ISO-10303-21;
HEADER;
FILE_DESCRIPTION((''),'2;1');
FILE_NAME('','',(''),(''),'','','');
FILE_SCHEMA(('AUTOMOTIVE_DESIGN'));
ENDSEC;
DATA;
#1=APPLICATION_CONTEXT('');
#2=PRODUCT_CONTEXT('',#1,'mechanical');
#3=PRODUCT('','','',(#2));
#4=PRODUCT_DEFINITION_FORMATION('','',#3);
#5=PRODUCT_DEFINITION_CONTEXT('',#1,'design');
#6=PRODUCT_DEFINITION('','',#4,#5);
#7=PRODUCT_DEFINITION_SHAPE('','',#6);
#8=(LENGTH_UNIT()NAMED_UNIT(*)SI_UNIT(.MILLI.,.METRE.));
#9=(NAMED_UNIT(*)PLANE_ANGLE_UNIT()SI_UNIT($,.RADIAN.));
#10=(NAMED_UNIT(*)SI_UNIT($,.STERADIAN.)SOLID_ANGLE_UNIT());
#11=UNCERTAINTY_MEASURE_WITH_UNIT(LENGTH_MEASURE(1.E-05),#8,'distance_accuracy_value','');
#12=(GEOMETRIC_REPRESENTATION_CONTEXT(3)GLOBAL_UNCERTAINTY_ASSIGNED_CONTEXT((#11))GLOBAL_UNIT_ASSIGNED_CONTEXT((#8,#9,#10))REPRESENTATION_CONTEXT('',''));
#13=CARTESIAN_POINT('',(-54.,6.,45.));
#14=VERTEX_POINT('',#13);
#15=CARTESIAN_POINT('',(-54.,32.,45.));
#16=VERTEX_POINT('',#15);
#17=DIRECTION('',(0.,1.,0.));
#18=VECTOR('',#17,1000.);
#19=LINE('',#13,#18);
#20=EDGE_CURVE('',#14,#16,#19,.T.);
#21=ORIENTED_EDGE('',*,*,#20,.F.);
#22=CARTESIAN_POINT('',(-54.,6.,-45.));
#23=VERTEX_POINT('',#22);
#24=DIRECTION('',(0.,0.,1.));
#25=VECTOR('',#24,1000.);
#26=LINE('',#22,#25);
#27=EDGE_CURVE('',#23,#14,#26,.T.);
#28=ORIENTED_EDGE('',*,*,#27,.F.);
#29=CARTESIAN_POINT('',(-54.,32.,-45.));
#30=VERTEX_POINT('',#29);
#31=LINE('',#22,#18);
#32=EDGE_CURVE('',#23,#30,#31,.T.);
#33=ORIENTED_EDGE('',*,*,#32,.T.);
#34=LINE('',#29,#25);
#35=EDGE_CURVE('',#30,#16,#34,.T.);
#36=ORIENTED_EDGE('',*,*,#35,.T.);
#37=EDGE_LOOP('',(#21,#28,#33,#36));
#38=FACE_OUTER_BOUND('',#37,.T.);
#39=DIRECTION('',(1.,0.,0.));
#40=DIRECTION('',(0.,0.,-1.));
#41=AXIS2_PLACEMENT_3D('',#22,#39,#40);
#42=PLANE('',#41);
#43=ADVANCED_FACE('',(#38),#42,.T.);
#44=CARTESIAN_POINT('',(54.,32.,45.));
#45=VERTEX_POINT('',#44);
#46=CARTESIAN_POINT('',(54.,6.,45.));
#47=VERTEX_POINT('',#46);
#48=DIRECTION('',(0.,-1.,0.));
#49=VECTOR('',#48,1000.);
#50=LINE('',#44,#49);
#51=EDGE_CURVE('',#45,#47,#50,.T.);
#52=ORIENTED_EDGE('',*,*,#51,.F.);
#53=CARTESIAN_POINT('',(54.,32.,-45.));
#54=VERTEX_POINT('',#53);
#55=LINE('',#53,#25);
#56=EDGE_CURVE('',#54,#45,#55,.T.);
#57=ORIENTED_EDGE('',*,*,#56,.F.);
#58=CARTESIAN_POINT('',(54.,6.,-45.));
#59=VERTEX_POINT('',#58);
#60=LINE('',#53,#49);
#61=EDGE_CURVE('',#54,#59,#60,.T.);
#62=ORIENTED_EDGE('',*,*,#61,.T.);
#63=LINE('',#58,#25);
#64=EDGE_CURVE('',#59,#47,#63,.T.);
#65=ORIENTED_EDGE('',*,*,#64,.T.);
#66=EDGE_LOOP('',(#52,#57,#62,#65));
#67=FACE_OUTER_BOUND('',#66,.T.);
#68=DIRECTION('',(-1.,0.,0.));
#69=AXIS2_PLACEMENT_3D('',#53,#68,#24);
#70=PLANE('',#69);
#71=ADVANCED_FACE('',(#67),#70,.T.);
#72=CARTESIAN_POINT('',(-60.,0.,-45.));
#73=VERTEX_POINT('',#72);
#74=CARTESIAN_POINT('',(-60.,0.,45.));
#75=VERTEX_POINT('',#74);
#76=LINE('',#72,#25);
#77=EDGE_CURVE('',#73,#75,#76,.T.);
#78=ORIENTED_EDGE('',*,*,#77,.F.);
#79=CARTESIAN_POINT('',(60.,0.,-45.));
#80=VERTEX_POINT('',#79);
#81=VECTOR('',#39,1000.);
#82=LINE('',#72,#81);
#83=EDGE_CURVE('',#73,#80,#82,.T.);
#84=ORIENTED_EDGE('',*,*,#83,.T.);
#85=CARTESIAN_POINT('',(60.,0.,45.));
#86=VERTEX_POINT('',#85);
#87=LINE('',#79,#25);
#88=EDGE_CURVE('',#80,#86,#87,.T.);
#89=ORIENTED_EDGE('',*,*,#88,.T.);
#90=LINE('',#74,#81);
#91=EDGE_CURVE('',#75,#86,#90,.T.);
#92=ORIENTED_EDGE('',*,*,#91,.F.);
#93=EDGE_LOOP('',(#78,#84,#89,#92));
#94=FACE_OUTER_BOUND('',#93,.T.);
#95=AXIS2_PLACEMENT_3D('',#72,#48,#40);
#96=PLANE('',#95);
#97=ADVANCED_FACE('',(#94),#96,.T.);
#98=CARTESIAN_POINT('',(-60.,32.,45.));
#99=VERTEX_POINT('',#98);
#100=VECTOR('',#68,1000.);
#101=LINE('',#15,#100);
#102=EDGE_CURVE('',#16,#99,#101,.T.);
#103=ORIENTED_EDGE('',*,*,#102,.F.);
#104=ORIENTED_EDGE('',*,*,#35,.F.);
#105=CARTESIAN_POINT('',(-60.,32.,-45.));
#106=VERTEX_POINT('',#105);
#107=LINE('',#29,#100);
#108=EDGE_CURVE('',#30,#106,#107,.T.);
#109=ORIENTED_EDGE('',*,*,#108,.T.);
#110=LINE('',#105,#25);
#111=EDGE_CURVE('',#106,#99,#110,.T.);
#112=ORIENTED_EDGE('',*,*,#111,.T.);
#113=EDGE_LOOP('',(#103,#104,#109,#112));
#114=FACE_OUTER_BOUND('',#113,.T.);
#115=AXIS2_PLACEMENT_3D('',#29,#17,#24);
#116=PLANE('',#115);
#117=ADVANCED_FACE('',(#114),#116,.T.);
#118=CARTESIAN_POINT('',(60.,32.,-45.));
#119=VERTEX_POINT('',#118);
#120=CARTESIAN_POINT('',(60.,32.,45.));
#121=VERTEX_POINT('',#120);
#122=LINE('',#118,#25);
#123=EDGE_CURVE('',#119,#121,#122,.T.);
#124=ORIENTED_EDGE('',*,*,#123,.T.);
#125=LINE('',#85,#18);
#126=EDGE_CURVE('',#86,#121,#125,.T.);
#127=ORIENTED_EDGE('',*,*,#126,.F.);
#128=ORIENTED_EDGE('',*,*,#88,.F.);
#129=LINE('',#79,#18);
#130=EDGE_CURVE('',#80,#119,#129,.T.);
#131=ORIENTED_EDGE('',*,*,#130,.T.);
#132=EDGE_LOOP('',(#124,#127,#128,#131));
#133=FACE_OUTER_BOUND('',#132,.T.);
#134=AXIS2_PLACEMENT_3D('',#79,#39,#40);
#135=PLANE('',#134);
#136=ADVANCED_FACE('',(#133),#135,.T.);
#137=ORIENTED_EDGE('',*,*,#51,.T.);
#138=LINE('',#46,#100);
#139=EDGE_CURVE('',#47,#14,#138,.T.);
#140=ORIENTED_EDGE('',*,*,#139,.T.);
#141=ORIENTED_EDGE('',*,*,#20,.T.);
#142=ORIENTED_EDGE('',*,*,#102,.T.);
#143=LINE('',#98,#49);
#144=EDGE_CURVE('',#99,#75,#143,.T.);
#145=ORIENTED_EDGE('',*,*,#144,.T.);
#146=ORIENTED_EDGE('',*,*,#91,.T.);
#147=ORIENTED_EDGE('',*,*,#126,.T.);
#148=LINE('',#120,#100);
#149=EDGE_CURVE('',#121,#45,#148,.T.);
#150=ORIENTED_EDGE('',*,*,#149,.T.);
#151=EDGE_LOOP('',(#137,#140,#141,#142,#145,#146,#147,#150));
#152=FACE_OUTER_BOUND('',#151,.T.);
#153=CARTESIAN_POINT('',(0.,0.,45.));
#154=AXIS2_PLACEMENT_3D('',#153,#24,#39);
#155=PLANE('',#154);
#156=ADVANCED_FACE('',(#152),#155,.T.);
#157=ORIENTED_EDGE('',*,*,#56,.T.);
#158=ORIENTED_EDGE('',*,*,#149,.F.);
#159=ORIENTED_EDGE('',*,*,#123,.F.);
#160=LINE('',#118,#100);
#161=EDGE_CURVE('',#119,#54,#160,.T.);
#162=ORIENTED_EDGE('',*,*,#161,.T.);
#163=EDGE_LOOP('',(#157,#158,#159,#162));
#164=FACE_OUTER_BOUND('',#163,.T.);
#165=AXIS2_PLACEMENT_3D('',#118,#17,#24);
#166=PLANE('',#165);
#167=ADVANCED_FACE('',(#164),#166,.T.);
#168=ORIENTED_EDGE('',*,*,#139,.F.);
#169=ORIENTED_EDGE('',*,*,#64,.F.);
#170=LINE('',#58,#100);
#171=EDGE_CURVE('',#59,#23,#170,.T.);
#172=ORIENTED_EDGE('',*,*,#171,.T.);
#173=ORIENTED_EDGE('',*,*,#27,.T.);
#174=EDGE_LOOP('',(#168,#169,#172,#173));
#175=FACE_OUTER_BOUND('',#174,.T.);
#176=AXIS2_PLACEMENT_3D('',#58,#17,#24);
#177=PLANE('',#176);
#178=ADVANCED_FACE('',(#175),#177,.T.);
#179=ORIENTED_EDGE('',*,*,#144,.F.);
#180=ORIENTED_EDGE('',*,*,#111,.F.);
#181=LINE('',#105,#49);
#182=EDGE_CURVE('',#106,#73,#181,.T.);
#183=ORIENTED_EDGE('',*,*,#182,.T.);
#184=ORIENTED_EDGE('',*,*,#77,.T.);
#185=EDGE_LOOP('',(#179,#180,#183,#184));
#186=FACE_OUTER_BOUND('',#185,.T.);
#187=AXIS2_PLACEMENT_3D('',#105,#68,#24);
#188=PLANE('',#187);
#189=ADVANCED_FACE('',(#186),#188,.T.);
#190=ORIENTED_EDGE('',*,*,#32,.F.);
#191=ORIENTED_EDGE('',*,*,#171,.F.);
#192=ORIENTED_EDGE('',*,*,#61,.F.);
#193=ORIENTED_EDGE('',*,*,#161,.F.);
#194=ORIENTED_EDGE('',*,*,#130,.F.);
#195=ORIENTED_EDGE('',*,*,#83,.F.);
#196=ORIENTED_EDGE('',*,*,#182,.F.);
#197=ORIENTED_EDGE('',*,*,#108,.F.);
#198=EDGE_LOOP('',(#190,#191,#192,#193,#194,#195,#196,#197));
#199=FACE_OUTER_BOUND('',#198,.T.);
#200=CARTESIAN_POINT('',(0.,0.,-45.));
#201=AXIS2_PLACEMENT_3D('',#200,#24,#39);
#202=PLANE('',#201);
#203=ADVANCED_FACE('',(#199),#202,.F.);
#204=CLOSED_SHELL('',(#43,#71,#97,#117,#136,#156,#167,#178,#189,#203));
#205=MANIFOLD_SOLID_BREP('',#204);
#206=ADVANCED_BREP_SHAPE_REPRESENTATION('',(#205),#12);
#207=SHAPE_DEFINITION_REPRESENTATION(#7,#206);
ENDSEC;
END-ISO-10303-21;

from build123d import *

# Parameters (mm, degrees)
EXTRUDE_1_DEPTH = 45


with BuildPart() as part:
    # 草图1 → 凸台-拉伸1 (new, symmetric)
    with BuildSketch(Plane.XY):
        Polygon((-60, 0), (60, 0), (60, 32), (54, 32), (54, 6), (-54, 6), (-54, 32), (-60, 32), align=None)
    extrude(amount=EXTRUDE_1_DEPTH, both=True)


solid = part.part
